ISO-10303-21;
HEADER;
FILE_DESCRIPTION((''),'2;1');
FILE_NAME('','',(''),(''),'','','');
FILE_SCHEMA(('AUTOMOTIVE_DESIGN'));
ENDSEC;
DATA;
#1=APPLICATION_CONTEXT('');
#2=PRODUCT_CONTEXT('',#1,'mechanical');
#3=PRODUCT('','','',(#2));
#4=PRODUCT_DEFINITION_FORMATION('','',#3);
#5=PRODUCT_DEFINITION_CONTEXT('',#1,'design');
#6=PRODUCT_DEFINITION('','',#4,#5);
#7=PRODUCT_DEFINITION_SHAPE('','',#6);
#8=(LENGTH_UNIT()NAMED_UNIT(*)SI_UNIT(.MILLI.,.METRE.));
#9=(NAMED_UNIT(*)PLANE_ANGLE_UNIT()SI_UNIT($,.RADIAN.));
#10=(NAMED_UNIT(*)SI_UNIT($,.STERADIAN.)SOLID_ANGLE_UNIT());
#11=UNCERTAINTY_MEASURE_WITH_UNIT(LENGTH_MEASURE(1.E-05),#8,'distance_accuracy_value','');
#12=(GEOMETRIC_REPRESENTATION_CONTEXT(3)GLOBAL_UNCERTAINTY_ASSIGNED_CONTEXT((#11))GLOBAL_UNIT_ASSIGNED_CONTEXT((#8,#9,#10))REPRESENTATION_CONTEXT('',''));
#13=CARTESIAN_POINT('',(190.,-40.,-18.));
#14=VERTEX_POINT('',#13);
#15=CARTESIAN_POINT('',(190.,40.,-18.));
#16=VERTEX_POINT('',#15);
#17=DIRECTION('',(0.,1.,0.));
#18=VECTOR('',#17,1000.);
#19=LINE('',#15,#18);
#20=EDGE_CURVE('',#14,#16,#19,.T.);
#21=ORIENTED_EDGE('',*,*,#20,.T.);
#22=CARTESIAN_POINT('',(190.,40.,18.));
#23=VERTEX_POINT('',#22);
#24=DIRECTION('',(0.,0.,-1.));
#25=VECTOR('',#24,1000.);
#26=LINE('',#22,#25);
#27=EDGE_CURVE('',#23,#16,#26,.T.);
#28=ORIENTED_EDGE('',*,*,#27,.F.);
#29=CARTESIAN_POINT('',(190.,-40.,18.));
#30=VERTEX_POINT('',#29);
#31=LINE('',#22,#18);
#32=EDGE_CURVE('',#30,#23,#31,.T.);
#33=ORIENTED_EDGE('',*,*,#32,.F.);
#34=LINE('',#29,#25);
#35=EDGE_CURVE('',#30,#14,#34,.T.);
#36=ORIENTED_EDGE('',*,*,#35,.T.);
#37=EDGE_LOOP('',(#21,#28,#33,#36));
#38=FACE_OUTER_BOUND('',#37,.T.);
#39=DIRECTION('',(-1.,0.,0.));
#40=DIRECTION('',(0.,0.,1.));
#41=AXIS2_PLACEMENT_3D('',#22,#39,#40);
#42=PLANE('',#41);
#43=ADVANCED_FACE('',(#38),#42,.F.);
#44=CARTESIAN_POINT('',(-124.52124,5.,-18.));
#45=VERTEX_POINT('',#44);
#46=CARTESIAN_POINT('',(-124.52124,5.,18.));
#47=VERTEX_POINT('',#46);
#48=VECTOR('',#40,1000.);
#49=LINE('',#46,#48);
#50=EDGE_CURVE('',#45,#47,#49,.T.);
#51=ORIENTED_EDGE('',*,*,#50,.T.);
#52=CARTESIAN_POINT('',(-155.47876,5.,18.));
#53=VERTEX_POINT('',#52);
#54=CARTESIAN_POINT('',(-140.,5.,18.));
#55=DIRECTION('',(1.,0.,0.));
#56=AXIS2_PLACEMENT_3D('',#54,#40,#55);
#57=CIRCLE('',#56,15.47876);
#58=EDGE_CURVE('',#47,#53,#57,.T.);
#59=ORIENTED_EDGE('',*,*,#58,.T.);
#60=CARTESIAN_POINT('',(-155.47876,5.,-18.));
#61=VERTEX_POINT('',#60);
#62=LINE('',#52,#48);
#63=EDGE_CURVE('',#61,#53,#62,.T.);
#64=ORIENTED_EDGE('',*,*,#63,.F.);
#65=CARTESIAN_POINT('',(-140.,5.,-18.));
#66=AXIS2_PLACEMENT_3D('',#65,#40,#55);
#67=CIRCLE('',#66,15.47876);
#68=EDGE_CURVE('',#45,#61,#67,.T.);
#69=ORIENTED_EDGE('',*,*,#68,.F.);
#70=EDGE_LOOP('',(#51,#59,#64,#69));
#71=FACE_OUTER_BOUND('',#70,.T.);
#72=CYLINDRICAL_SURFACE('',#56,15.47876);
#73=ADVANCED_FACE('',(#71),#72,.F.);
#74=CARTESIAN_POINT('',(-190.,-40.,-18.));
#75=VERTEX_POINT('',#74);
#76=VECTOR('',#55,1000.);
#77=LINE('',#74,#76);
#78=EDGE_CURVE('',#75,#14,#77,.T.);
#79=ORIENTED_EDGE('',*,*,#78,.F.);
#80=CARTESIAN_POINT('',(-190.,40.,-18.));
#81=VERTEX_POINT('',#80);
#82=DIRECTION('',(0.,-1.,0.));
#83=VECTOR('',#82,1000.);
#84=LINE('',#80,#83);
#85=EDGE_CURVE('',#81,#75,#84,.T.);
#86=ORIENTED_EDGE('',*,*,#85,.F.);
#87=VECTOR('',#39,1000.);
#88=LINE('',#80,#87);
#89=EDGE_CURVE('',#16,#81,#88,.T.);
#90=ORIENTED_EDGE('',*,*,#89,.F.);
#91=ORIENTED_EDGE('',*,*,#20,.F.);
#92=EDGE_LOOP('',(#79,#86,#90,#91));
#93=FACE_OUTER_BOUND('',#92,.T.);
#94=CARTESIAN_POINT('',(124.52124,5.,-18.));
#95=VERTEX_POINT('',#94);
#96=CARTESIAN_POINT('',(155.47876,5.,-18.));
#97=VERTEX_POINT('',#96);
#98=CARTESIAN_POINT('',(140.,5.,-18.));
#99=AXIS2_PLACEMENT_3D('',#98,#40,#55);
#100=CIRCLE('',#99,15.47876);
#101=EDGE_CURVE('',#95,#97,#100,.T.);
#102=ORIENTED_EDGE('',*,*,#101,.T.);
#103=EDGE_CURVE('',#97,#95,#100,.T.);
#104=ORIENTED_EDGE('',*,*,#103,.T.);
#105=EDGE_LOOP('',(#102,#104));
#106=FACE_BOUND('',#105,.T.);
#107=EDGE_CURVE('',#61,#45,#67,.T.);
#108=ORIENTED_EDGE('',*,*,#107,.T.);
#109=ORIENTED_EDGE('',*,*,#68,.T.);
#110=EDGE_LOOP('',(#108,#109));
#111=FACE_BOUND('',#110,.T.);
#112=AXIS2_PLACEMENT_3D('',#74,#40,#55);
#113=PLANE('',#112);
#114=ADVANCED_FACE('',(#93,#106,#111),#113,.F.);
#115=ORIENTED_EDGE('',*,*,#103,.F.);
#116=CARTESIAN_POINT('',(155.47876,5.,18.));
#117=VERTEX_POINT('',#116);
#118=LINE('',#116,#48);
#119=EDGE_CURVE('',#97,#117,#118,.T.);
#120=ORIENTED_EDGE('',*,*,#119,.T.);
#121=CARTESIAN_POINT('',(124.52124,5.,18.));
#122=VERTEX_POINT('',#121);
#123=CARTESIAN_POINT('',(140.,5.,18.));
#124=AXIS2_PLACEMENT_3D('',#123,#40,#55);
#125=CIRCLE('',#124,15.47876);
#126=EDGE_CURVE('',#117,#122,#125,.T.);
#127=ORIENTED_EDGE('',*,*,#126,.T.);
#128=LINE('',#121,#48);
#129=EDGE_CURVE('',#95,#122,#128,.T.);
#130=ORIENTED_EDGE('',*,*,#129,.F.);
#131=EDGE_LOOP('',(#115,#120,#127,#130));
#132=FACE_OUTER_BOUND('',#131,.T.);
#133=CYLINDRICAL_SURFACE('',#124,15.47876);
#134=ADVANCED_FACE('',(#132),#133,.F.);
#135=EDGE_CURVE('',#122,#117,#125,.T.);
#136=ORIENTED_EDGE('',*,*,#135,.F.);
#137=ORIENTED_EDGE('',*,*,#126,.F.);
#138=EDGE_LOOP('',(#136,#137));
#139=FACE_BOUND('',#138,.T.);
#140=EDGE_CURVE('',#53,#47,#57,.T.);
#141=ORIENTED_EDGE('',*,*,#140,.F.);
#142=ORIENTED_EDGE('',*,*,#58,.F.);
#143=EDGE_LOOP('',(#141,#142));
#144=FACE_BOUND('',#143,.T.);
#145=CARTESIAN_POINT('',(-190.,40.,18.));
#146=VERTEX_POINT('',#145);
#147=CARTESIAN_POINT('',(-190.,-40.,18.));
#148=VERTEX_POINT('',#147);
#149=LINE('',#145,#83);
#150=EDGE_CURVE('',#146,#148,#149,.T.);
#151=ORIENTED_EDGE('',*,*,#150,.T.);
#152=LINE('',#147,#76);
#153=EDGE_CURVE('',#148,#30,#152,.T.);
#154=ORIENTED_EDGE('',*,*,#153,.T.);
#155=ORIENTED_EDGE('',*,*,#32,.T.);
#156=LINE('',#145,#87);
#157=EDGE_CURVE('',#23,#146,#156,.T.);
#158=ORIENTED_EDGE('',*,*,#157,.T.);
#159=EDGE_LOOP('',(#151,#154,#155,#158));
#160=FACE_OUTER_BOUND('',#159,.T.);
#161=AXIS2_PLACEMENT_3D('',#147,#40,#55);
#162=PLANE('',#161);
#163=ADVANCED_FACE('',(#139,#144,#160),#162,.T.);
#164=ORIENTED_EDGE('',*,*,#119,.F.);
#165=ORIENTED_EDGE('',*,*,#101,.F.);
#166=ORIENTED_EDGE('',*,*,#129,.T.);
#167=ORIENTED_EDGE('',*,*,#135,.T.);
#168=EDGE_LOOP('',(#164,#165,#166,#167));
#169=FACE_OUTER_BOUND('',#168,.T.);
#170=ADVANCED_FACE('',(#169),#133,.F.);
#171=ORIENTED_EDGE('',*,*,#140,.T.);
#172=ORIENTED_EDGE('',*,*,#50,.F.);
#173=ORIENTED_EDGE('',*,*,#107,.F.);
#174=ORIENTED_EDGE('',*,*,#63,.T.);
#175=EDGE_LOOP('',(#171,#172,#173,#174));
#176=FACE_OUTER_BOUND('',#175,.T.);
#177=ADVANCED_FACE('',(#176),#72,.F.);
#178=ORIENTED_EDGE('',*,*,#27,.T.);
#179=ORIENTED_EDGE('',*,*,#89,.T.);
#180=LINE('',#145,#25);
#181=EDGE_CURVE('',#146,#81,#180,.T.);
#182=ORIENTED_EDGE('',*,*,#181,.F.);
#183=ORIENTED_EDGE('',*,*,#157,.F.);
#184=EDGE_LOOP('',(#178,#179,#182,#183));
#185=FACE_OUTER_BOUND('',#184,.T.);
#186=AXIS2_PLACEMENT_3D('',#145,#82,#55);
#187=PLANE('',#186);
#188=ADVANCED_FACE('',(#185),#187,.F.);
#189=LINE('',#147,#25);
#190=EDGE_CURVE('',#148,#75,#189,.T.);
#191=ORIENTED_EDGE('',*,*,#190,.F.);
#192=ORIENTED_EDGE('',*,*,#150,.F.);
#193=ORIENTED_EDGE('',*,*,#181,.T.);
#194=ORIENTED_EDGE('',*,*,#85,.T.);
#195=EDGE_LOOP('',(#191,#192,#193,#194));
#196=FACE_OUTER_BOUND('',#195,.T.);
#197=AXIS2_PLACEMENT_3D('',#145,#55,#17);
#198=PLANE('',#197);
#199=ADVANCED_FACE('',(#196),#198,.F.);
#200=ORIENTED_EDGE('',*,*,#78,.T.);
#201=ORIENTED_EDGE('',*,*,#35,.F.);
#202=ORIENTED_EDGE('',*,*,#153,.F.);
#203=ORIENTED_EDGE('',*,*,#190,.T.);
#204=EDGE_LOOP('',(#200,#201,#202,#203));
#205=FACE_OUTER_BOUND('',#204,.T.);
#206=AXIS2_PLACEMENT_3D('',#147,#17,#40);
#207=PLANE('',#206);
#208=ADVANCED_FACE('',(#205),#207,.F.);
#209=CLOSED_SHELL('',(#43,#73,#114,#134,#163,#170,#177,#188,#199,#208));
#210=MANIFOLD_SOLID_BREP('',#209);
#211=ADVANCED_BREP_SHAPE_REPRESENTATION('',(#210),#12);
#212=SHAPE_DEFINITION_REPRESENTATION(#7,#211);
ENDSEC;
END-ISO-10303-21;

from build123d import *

# Parameters (mm, degrees)
SKETCH1_W                = 380
SKETCH1_H                = 80
BOSS_EXTRUDE1_DEPTH      = 18
F_1_3_8_6_TAPPED_HOLE1_D = 30.95752


with BuildPart() as part:
    # Sketch1 → Boss-Extrude1 (new, symmetric)
    with BuildSketch(Plane.XY):
        Rectangle(SKETCH1_W, SKETCH1_H)
    extrude(amount=BOSS_EXTRUDE1_DEPTH, both=True)

    # 1-3/8-6 Tapped Hole1 (through all)
    with Locations(Plane.XY.offset(18)):
        with Locations((-140, 5), (140, 5)):
            Hole(F_1_3_8_6_TAPPED_HOLE1_D / 2)


solid = part.part
